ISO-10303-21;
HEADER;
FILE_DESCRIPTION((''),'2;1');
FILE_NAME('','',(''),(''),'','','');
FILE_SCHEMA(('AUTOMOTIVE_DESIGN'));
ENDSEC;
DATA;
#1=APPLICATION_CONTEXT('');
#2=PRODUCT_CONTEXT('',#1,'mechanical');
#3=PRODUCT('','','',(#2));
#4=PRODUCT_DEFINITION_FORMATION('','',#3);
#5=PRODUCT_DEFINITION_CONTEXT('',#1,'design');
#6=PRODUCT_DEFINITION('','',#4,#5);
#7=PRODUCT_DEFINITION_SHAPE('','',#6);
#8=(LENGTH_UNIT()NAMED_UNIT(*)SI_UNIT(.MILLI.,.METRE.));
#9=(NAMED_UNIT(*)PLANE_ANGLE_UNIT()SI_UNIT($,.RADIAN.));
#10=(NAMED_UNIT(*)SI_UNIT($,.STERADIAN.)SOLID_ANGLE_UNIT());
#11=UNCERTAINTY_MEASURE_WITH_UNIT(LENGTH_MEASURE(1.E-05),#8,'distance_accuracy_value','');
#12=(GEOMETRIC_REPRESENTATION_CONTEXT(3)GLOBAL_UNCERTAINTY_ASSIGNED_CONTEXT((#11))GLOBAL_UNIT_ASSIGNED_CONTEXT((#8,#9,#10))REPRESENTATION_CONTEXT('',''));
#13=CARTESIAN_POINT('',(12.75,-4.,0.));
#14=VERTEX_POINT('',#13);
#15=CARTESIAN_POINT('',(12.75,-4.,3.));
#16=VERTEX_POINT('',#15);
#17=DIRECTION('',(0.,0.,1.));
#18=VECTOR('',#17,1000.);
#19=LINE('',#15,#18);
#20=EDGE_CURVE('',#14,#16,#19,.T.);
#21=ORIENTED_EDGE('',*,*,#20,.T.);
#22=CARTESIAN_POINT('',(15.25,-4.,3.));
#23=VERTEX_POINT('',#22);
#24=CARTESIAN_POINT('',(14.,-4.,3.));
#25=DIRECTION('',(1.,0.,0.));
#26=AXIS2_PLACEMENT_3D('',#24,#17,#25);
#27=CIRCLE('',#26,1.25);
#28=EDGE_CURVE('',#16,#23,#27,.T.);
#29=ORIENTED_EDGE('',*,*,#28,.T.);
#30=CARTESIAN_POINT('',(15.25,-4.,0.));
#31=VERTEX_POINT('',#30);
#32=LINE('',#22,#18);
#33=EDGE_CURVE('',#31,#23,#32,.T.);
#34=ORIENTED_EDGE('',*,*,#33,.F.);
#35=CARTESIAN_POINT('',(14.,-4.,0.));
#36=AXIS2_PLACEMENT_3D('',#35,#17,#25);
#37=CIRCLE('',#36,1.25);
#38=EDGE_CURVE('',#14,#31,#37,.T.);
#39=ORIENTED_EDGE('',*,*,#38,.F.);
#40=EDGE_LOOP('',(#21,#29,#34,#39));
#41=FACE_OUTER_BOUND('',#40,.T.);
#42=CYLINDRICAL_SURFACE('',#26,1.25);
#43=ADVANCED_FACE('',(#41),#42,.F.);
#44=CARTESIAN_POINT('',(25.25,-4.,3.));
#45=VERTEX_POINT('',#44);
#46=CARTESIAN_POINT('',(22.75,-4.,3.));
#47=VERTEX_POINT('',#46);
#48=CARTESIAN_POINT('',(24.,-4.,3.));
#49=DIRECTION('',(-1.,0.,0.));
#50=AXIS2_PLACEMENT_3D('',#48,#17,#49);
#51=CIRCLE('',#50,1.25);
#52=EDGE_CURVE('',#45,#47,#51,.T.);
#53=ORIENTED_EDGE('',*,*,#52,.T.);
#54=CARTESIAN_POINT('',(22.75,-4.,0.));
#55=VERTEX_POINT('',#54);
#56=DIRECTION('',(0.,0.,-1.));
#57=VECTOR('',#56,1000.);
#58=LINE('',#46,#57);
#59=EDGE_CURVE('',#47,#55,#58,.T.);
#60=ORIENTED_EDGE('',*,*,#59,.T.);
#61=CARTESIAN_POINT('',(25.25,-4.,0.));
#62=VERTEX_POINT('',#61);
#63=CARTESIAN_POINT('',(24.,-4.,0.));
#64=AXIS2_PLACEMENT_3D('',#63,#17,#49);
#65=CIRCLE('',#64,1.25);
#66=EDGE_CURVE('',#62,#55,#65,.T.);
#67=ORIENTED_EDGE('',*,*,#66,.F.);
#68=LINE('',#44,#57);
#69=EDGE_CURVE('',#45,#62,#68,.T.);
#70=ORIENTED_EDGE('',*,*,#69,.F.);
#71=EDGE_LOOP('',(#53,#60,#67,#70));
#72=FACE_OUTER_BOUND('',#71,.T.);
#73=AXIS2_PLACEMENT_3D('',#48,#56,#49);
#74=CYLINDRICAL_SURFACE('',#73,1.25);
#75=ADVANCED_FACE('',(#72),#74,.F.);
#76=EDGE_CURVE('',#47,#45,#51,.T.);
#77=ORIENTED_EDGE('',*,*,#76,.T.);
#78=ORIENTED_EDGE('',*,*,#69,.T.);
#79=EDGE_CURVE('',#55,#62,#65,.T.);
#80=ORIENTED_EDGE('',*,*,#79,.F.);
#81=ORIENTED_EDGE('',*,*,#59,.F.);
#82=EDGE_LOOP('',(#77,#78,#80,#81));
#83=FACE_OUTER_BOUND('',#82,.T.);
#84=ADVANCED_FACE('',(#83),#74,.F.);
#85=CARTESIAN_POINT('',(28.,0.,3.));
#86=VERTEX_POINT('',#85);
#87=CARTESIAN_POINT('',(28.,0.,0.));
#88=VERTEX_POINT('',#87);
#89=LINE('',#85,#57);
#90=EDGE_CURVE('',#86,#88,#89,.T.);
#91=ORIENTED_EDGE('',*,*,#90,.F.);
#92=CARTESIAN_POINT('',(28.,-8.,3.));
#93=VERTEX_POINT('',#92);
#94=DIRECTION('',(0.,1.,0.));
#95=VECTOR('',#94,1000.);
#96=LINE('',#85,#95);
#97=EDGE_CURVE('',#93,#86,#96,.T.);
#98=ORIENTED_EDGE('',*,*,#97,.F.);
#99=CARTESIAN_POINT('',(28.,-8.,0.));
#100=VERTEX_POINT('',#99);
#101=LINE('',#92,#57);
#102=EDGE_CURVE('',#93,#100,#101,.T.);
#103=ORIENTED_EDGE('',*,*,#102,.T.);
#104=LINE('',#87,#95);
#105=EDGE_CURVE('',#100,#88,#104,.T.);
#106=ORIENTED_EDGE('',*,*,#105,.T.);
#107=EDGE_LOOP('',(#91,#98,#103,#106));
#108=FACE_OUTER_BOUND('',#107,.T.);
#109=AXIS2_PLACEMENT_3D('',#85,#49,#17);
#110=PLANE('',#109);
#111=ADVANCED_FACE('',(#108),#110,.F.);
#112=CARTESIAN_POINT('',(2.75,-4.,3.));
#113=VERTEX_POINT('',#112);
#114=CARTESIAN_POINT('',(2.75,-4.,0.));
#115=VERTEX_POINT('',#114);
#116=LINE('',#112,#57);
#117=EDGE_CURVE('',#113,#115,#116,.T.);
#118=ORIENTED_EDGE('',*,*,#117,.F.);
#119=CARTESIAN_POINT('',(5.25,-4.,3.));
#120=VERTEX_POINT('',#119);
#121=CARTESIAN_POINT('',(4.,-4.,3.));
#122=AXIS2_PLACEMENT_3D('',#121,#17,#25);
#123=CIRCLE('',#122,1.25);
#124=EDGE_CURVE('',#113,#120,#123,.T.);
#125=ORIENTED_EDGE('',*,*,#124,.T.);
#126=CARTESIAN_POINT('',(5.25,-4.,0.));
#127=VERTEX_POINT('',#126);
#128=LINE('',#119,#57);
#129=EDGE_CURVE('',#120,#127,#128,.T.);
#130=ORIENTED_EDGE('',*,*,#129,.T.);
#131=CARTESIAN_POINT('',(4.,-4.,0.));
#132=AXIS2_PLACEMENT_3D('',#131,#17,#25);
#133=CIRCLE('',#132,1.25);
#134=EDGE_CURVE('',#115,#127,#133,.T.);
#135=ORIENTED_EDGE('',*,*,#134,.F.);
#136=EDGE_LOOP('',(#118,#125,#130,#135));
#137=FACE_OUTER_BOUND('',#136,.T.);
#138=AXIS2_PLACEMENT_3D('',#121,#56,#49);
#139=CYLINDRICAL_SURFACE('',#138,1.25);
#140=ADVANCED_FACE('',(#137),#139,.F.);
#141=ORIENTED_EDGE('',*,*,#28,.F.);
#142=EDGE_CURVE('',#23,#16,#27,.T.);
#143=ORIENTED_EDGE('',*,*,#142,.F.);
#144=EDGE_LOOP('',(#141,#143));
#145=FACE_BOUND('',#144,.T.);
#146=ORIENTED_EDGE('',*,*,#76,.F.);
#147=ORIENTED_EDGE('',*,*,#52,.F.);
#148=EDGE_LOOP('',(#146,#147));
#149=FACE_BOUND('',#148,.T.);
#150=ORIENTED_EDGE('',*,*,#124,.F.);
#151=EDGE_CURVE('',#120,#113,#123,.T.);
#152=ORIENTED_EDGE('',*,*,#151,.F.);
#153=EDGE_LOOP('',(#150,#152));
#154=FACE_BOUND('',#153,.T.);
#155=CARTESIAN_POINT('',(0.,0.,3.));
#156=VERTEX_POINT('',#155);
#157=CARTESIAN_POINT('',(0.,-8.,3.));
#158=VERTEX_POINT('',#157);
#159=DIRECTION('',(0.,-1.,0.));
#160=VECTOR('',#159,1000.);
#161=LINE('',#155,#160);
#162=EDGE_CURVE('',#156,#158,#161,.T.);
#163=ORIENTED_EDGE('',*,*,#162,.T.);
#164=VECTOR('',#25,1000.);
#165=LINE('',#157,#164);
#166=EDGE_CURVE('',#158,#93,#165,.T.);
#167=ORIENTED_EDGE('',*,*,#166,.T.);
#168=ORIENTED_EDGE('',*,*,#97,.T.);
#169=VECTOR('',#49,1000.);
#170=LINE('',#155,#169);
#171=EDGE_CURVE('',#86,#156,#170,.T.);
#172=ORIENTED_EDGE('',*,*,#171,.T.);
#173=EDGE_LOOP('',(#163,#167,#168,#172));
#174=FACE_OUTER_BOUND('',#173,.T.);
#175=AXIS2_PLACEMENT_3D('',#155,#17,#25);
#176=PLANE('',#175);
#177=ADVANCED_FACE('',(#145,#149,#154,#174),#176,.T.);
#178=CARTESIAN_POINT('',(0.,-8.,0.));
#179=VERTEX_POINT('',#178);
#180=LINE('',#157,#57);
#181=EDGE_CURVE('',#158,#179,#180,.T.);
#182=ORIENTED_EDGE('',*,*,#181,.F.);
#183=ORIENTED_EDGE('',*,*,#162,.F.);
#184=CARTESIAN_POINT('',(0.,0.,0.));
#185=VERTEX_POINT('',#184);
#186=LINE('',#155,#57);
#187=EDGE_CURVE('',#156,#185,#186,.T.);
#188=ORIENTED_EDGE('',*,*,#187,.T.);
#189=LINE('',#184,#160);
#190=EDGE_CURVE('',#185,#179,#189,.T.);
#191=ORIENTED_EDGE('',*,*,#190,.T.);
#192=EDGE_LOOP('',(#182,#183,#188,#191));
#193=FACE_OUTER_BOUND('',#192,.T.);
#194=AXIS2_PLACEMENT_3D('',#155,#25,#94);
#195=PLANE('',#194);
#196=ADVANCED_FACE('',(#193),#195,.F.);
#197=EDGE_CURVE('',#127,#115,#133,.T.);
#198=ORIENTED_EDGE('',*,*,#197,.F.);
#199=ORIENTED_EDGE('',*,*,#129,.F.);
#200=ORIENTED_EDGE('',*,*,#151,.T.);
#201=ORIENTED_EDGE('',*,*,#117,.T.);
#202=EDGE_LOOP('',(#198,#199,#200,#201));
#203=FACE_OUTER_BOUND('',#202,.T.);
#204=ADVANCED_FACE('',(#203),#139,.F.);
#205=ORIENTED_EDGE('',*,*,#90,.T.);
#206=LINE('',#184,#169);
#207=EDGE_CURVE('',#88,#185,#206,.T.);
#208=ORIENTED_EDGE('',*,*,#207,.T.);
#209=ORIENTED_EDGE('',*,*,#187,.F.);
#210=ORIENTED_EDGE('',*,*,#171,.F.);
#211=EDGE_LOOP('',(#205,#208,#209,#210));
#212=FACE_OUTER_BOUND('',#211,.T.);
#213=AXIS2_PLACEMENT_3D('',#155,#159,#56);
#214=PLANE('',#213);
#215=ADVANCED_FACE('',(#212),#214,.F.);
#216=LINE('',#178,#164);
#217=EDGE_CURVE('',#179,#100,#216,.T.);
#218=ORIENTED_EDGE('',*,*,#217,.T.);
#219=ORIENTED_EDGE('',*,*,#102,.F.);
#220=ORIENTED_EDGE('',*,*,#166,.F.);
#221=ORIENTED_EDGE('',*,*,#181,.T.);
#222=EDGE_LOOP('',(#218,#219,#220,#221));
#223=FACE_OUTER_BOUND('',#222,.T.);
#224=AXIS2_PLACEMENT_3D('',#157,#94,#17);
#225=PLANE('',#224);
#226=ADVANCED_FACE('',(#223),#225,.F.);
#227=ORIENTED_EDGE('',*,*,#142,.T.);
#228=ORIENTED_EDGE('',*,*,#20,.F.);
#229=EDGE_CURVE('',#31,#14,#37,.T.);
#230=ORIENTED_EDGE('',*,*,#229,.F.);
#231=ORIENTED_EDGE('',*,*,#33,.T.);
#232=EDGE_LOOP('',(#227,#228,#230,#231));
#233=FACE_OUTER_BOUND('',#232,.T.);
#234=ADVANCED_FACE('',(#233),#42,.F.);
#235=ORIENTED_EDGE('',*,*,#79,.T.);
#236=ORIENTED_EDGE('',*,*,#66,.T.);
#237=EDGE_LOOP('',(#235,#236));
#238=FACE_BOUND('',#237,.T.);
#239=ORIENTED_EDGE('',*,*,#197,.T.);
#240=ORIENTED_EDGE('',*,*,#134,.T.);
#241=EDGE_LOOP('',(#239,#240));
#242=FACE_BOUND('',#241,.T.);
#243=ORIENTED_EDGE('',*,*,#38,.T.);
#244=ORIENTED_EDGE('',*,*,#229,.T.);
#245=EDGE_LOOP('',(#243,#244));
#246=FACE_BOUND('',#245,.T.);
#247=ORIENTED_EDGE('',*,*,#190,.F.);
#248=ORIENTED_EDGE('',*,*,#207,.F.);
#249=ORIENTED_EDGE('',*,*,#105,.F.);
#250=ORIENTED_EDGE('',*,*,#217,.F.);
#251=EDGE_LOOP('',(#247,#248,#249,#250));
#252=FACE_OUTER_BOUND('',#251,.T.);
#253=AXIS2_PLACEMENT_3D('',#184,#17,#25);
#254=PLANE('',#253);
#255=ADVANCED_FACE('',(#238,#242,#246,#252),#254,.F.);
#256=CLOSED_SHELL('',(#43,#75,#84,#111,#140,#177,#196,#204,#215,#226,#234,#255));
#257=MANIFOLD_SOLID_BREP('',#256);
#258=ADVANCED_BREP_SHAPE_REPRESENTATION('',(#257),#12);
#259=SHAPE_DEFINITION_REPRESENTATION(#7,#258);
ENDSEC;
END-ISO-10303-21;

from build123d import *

# Parameters (mm, degrees)
SKETCH1_W             = 28
SKETCH1_H             = 8
SKETCH1_R             = 1.25
BOSS_EXTRUDE1_DEPTH   = 3
M3_TAPPED_HOLE6_D     = 2.5
M3_TAPPED_HOLE6_DEPTH = 7.5
M3_TAPPED_HOLE6_TIP   = 0.751075774
M3_TAPPED_HOLE1_D     = 2.5
M3_TAPPED_HOLE1_DEPTH = 7.5
M3_TAPPED_HOLE1_TIP   = 0.751075774


with BuildPart() as part:
    # Sketch1 → Boss-Extrude1 (new body)
    with BuildSketch(Plane.XY):
        with Locations((14, -4)):
            Rectangle(SKETCH1_W, SKETCH1_H)
        with Locations((4, -4)):
            Circle(SKETCH1_R, mode=Mode.SUBTRACT)
        with Locations(Location((24, -4, 0), (0, 0, 180))):
            Circle(SKETCH1_R, mode=Mode.SUBTRACT)
    extrude(amount=BOSS_EXTRUDE1_DEPTH)

    # M3 Tapped Hole6
    with Locations(Plane(origin=(4, -4, 3), x_dir=(1, 0, 0), z_dir=(0, 0, 1))):
        with Locations((0, 0), (20, 0)):
            Hole(M3_TAPPED_HOLE6_D / 2, depth=M3_TAPPED_HOLE6_DEPTH)
            with Locations((0, 0, -(M3_TAPPED_HOLE6_DEPTH + M3_TAPPED_HOLE6_TIP / 2))):  # 118° drill point
                Cone(0, M3_TAPPED_HOLE6_D / 2, M3_TAPPED_HOLE6_TIP, mode=Mode.SUBTRACT)

    # M3 Tapped Hole1
    with Locations(Plane(origin=(14, -4, 3), x_dir=(1, 0, 0), z_dir=(0, 0, 1))):
        with Locations((0, 0)):
            Hole(M3_TAPPED_HOLE1_D / 2, depth=M3_TAPPED_HOLE1_DEPTH)
            with Locations((0, 0, -(M3_TAPPED_HOLE1_DEPTH + M3_TAPPED_HOLE1_TIP / 2))):  # 118° drill point
                Cone(0, M3_TAPPED_HOLE1_D / 2, M3_TAPPED_HOLE1_TIP, mode=Mode.SUBTRACT)


solid = part.part
